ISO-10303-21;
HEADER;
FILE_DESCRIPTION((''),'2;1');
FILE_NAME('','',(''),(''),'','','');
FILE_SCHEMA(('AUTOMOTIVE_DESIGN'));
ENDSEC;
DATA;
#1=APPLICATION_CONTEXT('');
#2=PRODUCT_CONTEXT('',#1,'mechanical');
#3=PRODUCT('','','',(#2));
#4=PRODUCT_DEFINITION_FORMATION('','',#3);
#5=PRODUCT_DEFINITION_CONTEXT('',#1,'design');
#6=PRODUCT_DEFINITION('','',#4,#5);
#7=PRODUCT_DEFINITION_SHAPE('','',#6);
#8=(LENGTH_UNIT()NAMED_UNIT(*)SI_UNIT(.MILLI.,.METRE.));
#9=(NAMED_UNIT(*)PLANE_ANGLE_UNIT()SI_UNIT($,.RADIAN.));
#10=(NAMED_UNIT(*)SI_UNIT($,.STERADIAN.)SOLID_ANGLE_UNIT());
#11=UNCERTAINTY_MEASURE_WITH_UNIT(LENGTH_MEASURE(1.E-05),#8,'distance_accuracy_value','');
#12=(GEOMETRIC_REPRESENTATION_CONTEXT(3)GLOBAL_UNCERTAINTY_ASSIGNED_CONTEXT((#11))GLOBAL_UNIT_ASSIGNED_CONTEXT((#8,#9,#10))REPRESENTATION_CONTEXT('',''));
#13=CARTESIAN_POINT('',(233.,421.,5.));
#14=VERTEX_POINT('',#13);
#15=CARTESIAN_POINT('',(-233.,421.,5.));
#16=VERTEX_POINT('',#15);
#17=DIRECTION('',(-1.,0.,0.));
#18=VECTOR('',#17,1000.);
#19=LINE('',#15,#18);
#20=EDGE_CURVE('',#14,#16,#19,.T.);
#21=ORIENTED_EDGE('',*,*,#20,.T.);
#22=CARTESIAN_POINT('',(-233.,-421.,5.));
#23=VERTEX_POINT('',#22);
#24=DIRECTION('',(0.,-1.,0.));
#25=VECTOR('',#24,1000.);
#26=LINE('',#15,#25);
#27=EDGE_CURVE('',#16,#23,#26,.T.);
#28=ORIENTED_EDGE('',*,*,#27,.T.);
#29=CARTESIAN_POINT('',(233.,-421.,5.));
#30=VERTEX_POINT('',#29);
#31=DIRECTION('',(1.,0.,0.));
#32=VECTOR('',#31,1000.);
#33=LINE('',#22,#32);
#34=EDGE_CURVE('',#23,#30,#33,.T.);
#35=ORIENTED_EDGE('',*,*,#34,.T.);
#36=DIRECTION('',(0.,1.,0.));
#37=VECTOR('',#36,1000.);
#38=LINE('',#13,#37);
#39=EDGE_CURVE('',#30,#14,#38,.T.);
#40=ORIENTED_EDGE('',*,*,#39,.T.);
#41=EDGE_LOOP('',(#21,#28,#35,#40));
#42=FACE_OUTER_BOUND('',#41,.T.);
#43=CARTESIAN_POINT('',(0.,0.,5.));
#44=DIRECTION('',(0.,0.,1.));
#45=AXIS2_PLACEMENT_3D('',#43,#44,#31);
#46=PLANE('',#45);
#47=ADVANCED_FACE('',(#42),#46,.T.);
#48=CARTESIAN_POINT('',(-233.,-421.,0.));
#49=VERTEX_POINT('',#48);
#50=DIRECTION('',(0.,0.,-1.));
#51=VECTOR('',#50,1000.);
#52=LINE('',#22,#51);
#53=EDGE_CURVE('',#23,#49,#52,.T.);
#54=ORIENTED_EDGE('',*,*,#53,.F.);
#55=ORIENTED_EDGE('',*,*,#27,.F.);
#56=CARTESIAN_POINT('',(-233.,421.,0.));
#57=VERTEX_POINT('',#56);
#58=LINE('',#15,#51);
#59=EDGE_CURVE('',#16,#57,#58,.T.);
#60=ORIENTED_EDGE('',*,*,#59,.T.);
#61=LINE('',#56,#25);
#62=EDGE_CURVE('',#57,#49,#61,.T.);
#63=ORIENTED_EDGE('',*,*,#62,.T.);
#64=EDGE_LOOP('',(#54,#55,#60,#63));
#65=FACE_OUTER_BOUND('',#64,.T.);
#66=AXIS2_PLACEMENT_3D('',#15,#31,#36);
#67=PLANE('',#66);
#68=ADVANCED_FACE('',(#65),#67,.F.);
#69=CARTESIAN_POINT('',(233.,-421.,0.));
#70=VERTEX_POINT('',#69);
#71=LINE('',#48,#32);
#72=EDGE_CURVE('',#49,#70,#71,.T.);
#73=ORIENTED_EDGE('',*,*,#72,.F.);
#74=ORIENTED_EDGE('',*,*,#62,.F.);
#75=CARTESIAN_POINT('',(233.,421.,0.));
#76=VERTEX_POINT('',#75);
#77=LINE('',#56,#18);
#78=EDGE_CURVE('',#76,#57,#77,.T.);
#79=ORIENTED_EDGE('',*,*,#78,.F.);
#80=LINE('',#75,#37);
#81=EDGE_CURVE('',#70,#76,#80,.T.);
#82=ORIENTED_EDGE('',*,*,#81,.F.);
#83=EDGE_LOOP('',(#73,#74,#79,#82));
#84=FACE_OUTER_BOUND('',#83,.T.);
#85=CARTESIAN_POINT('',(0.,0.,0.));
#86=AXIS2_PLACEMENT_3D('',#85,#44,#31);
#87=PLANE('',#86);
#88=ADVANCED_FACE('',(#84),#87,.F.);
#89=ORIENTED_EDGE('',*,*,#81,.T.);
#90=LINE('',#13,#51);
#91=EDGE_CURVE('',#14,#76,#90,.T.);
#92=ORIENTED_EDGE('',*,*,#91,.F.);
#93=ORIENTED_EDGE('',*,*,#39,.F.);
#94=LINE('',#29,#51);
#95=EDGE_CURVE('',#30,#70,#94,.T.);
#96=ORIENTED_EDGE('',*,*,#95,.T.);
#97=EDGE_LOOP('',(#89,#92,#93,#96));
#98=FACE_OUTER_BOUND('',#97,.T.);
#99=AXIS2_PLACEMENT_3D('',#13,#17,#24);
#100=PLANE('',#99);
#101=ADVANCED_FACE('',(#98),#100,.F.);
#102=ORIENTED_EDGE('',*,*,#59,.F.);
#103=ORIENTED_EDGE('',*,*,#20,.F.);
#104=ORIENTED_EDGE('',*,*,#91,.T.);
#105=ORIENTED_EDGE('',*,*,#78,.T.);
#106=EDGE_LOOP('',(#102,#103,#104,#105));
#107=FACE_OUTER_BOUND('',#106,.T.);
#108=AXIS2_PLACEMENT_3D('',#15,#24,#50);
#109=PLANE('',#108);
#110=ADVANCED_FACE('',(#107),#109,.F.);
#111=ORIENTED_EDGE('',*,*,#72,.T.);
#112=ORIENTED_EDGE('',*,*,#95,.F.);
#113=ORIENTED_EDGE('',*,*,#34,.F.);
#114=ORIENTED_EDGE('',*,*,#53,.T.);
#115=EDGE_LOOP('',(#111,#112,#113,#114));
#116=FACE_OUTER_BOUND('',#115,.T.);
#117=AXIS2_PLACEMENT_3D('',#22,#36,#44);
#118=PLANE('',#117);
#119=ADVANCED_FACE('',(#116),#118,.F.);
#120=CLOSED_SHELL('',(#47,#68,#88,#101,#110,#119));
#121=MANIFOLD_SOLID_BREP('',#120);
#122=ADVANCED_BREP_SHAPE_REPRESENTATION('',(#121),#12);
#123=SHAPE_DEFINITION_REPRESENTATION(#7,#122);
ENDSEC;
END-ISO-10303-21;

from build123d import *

# Parameters (mm, degrees)
SKETCH_1_W      = 466
SKETCH_1_H      = 842
EXTRUDE_1_DEPTH = 5


with BuildPart() as part:
    # 草图1 → 凸台-拉伸1 (new body)
    with BuildSketch(Plane.XY):
        Rectangle(SKETCH_1_W, SKETCH_1_H)
    extrude(amount=EXTRUDE_1_DEPTH)


solid = part.part
